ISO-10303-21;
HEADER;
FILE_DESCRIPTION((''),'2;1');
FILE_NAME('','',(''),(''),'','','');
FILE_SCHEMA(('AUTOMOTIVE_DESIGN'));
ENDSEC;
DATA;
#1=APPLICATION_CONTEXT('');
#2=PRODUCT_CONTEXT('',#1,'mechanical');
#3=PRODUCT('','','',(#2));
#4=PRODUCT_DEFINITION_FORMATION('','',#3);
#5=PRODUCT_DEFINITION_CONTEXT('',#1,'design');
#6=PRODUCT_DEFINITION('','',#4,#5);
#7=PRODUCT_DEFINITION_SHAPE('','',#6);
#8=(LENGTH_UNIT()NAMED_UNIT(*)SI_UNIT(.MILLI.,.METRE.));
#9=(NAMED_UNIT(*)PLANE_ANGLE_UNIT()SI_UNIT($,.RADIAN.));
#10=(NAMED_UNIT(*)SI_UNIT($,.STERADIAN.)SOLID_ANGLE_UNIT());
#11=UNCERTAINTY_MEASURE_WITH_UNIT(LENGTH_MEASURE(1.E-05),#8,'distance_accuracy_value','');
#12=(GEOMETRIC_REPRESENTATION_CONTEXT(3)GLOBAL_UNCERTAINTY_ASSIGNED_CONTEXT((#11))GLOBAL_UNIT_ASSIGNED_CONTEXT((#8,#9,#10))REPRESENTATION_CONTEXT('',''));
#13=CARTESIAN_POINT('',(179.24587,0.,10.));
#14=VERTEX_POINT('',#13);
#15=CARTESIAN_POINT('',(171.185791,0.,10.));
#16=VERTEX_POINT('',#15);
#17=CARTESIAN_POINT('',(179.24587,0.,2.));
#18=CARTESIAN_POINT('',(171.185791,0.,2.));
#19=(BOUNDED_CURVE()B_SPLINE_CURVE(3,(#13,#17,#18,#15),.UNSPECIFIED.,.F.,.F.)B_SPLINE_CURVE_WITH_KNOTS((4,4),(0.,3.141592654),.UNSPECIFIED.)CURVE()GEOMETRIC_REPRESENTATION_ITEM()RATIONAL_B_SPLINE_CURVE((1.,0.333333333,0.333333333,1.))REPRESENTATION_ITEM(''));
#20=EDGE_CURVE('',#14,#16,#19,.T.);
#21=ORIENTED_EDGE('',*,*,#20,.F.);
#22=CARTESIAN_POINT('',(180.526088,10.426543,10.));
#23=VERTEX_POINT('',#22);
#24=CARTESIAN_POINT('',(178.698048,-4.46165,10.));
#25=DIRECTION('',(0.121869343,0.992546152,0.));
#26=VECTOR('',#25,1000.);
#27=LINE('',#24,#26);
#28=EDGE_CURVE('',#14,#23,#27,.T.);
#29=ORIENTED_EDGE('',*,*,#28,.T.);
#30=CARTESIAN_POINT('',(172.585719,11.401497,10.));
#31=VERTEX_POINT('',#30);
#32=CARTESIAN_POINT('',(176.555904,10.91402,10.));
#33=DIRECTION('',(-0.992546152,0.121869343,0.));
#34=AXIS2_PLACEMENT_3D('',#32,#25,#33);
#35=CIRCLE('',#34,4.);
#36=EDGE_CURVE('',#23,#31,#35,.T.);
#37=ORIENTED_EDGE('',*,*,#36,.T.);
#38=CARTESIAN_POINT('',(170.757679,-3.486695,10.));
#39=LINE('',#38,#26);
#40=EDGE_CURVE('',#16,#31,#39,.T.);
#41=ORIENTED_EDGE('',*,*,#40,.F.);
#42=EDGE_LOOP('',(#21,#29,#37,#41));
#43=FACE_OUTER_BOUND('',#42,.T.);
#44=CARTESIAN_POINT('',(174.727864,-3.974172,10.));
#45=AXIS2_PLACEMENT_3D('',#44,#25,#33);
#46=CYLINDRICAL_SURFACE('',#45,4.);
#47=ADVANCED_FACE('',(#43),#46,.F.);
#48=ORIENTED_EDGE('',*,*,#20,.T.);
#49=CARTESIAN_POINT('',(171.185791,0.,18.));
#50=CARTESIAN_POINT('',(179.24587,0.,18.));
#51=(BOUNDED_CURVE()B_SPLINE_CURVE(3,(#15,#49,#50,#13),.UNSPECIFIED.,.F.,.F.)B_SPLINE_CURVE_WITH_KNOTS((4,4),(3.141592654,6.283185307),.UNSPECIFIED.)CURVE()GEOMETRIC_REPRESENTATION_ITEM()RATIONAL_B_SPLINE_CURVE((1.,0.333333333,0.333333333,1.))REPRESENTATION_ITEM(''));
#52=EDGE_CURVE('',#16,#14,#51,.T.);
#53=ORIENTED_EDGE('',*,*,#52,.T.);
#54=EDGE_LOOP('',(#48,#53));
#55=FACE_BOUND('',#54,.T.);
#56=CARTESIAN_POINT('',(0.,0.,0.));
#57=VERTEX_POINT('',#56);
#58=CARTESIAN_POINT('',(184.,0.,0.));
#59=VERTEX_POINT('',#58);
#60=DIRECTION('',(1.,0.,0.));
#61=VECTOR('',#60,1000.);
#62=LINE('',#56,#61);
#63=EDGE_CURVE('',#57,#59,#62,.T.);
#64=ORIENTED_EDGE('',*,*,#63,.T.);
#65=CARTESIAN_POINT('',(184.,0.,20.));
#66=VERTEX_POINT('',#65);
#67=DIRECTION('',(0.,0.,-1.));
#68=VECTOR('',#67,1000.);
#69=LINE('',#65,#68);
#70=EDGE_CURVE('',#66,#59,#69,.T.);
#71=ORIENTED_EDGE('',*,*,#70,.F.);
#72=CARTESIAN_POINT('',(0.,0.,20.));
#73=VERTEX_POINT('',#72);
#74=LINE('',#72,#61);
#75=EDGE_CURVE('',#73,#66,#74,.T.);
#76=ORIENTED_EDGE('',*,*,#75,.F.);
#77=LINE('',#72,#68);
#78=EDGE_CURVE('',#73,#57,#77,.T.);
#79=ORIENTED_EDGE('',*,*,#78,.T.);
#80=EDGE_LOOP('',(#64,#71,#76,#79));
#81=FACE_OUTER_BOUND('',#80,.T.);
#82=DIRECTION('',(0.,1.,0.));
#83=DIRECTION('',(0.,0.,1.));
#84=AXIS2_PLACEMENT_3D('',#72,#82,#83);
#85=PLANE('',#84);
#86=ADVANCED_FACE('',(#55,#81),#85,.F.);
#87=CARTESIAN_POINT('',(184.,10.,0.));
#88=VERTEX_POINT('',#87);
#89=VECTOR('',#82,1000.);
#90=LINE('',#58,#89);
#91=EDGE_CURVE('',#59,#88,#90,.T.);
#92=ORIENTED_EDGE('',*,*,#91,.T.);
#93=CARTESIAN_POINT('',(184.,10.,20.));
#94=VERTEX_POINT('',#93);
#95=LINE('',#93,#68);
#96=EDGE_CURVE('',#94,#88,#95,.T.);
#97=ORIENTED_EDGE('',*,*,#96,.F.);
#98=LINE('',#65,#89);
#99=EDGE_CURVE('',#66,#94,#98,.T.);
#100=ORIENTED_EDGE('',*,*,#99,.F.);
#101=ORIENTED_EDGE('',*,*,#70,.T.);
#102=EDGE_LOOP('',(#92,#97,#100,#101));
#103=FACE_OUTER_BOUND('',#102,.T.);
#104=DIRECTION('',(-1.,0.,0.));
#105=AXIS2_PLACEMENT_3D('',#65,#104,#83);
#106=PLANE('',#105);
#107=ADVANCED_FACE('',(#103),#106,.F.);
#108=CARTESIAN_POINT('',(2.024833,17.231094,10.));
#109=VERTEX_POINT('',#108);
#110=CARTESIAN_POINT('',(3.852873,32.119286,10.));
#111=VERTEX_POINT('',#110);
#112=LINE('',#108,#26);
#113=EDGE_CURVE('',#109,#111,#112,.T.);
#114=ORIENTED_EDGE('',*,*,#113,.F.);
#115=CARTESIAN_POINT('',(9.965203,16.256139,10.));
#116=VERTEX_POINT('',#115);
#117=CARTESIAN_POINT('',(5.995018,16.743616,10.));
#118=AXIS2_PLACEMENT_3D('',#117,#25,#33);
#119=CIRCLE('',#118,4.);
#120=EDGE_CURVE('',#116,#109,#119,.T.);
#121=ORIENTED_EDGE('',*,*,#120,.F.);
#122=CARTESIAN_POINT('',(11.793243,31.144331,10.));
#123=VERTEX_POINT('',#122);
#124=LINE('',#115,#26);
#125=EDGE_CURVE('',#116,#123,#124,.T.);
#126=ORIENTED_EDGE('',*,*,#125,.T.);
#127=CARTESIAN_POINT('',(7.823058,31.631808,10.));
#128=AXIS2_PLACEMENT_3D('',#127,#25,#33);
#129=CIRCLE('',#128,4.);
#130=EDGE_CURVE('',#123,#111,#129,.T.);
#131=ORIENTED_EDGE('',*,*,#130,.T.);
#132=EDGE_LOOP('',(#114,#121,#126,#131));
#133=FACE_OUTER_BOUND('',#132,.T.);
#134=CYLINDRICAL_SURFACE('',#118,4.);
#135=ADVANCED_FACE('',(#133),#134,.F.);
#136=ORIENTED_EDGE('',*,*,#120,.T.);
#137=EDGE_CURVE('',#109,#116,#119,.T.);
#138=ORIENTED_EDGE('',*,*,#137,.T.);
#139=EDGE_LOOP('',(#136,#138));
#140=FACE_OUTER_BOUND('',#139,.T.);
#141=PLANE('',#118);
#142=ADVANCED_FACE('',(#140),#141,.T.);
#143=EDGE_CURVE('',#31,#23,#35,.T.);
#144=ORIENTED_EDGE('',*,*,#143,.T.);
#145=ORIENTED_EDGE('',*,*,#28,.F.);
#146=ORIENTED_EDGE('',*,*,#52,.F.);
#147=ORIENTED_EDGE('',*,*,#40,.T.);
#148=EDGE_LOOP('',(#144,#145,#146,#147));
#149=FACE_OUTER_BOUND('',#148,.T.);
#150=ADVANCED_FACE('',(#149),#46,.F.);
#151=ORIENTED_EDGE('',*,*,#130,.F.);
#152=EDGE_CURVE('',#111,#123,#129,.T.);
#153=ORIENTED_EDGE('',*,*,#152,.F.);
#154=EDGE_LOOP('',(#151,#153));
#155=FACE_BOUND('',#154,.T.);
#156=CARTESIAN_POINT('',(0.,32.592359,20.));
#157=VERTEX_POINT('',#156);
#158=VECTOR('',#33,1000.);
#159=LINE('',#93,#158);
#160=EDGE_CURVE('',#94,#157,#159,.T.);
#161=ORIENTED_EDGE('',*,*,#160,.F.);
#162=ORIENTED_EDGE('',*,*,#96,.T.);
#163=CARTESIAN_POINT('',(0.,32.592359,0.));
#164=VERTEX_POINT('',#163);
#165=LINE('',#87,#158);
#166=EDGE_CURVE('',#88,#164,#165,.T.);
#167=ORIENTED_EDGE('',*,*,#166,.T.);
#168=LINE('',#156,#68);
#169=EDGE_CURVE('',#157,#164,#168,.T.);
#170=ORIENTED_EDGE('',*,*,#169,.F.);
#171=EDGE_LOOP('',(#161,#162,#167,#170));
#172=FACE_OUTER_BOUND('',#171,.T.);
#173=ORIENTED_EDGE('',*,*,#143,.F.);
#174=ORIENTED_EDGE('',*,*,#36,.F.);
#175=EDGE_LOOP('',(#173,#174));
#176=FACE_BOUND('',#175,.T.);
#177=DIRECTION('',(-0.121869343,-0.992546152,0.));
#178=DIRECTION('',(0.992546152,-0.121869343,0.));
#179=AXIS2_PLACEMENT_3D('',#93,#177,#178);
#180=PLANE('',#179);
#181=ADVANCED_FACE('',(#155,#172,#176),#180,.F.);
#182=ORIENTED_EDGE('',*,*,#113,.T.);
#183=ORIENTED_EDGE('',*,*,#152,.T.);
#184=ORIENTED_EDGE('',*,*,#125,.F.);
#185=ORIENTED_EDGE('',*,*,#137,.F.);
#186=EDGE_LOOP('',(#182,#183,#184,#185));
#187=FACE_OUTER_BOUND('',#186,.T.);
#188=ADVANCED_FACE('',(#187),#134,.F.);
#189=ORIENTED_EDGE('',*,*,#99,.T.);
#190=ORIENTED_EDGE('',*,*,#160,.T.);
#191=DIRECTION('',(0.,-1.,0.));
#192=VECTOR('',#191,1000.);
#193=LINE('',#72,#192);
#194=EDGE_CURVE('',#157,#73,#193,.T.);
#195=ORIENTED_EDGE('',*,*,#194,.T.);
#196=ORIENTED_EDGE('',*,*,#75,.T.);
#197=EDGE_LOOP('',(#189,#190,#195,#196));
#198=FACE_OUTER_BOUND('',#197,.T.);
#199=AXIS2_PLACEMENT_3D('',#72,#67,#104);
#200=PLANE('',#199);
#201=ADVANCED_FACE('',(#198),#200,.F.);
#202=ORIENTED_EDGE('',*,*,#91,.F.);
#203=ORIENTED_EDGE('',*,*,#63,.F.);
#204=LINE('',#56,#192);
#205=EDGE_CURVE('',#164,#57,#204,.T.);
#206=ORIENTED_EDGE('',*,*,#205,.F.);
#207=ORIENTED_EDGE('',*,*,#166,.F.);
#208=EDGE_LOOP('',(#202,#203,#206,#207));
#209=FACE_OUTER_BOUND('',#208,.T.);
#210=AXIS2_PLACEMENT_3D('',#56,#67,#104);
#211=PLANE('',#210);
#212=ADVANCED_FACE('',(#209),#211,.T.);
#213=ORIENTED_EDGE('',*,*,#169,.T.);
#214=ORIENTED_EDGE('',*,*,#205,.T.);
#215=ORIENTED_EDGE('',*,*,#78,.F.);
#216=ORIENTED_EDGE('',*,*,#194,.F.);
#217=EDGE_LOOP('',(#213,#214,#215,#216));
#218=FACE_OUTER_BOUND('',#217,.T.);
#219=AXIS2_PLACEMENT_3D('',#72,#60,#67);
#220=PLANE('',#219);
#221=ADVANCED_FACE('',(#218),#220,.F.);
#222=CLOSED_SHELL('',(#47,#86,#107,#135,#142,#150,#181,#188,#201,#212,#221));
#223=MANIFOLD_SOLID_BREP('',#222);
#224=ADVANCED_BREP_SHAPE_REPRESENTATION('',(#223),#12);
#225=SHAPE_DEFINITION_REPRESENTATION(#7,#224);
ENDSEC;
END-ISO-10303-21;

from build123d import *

# Parameters (mm, degrees)
BOSS_EXTRUDE1_DEPTH = 20
SKETCH2_R           = 4
CUT_EXTRUDE1_DEPTH  = 15
LPATTERN1_COUNT     = 2
LPATTERN1_PITCH     = 170


with BuildPart() as part:
    # Sketch1 → Boss-Extrude1 (new body)
    with BuildSketch(Plane.XY):
        Polygon((0, 0), (184, 0), (184, 10), (0, 32.592359206), align=None)
    extrude(amount=BOSS_EXTRUDE1_DEPTH)

    # Sketch2 → Cut-Extrude1 (cut)
    with BuildSketch(Plane(origin=(3.942402661, 32.108293027, 0), x_dir=(0.9925461516413229, -0.12186934340514068, 0), z_dir=(0.12186934340514069, 0.992546151641323, 0))):
        with Locations(Location((173.909798468, -10, 0), (0, 0, 180))):
            Circle(SKETCH2_R)
    cut_extrude1 = extrude(amount=-CUT_EXTRUDE1_DEPTH, mode=Mode.SUBTRACT)

    # LPattern1: Cut-Extrude1 ×2
    with Locations(*[Vector(-0.9925461516413229, 0.12186934340514068, 0) * (i * LPATTERN1_PITCH) for i in range(1, LPATTERN1_COUNT)]):
        add(cut_extrude1, mode=Mode.SUBTRACT)


solid = part.part
